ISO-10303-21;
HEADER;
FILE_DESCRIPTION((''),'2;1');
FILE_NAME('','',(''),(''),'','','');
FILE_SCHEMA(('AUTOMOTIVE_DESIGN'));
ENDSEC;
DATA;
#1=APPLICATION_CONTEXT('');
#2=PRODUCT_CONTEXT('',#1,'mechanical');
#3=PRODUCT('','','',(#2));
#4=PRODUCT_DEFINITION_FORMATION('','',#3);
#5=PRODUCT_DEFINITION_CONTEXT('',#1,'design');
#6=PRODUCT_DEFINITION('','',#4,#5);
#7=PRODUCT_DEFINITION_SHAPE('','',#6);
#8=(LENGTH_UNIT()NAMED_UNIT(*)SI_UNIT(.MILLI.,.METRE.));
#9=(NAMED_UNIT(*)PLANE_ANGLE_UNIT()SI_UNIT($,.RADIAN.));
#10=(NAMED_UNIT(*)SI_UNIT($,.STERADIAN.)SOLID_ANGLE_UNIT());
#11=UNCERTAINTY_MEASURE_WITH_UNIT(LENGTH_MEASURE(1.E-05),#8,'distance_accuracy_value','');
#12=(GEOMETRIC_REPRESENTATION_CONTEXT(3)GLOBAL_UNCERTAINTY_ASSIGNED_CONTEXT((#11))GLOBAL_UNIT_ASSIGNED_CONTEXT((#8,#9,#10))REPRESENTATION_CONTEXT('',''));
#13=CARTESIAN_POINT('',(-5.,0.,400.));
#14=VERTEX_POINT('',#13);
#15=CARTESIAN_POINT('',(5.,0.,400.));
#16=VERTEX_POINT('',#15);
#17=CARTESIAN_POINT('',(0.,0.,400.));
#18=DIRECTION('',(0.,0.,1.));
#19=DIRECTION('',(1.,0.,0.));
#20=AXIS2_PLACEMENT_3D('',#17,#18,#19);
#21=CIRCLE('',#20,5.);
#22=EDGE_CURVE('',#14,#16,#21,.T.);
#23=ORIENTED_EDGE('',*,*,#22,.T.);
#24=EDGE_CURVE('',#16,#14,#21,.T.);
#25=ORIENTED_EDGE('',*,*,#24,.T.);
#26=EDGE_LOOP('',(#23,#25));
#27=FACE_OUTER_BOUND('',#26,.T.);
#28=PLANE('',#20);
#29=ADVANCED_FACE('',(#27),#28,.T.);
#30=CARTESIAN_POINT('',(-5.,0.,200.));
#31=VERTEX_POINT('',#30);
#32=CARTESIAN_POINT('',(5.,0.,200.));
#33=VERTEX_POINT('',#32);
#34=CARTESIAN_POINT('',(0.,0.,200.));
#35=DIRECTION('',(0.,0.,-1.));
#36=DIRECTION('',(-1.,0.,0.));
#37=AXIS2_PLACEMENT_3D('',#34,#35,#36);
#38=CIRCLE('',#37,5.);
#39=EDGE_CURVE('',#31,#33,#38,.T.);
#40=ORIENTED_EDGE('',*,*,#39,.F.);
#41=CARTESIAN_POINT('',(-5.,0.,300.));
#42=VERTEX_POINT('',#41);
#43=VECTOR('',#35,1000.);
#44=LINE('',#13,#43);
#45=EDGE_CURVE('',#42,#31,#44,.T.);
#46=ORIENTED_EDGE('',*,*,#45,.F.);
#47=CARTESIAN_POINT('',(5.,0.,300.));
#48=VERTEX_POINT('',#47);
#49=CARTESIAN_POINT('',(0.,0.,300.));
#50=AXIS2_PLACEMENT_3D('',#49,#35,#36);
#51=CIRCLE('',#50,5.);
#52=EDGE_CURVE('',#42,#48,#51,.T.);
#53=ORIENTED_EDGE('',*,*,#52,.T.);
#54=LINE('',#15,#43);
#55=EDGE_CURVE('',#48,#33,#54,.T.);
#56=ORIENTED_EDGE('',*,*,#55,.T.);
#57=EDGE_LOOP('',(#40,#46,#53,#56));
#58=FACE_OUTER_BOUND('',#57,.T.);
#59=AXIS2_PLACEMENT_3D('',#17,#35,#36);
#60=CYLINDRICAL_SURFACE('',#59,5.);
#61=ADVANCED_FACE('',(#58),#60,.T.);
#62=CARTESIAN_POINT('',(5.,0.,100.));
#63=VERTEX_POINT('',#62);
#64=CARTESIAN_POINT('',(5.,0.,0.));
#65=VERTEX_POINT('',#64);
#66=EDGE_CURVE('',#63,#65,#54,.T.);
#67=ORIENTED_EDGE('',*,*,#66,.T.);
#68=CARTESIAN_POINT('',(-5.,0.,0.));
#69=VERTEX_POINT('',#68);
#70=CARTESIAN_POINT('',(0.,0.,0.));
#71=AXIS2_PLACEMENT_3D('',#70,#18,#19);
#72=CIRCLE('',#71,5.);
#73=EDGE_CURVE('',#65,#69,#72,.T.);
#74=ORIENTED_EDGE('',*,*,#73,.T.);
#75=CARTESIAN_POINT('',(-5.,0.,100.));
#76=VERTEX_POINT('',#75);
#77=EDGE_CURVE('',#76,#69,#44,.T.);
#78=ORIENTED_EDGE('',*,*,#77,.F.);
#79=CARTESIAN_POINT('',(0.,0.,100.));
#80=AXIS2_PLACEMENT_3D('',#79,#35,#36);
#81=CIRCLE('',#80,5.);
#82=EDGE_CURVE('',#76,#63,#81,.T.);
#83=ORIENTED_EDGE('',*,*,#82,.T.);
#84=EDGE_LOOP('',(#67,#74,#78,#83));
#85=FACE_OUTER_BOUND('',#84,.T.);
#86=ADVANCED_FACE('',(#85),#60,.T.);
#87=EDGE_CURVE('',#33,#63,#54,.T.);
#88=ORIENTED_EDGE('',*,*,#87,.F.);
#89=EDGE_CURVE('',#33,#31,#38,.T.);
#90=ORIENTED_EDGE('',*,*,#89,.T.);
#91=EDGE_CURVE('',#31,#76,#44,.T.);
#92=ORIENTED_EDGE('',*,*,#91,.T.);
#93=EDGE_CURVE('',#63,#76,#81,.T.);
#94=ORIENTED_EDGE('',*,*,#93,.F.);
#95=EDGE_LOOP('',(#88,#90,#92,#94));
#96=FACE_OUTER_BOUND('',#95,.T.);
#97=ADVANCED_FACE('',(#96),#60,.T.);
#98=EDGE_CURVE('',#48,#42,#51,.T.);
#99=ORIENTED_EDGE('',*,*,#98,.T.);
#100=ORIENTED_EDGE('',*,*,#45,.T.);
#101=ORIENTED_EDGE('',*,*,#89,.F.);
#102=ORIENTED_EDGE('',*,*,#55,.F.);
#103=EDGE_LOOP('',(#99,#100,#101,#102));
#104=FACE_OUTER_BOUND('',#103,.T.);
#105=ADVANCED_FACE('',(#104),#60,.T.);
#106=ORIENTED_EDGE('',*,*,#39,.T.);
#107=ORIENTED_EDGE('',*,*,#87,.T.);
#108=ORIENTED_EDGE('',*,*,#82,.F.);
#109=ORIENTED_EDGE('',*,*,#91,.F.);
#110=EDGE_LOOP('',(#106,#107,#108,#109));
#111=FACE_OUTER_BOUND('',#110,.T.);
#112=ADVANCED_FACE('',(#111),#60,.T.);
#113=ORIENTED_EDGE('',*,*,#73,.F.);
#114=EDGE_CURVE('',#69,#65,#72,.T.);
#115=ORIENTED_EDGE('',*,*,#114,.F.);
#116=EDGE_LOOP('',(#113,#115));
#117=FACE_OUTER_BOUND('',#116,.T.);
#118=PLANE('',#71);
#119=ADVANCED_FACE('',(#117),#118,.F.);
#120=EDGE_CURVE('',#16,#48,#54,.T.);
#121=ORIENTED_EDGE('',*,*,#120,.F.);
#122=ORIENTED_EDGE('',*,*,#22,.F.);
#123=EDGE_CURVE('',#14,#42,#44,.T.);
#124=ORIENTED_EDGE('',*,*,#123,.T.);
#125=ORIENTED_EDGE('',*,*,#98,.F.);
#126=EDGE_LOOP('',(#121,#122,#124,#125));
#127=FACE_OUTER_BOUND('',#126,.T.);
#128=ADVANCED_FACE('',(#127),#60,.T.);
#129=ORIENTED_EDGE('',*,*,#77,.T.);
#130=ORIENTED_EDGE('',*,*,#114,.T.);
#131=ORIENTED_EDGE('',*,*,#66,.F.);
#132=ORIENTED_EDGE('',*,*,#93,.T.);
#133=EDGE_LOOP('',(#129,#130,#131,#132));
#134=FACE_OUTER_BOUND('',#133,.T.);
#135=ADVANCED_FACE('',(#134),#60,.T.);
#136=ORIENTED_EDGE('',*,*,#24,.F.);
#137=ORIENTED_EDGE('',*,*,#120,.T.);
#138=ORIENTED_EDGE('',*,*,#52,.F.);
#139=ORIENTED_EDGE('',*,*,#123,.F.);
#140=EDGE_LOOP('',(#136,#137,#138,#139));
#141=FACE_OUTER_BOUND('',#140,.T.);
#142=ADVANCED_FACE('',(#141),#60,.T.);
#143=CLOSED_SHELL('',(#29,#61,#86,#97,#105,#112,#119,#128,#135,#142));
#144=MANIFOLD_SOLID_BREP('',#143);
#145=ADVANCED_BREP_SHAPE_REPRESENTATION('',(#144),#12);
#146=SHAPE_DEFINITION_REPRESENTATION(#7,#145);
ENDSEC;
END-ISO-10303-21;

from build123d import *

# Parameters (mm, degrees)
SKETCH1_R           = 5
BOSS_EXTRUDE1_DEPTH = 400


with BuildPart() as part:
    # Sketch1 → Boss-Extrude1 (new body)
    with BuildSketch(Plane.XY):
        Circle(SKETCH1_R)
    extrude(amount=BOSS_EXTRUDE1_DEPTH)


solid = part.part
